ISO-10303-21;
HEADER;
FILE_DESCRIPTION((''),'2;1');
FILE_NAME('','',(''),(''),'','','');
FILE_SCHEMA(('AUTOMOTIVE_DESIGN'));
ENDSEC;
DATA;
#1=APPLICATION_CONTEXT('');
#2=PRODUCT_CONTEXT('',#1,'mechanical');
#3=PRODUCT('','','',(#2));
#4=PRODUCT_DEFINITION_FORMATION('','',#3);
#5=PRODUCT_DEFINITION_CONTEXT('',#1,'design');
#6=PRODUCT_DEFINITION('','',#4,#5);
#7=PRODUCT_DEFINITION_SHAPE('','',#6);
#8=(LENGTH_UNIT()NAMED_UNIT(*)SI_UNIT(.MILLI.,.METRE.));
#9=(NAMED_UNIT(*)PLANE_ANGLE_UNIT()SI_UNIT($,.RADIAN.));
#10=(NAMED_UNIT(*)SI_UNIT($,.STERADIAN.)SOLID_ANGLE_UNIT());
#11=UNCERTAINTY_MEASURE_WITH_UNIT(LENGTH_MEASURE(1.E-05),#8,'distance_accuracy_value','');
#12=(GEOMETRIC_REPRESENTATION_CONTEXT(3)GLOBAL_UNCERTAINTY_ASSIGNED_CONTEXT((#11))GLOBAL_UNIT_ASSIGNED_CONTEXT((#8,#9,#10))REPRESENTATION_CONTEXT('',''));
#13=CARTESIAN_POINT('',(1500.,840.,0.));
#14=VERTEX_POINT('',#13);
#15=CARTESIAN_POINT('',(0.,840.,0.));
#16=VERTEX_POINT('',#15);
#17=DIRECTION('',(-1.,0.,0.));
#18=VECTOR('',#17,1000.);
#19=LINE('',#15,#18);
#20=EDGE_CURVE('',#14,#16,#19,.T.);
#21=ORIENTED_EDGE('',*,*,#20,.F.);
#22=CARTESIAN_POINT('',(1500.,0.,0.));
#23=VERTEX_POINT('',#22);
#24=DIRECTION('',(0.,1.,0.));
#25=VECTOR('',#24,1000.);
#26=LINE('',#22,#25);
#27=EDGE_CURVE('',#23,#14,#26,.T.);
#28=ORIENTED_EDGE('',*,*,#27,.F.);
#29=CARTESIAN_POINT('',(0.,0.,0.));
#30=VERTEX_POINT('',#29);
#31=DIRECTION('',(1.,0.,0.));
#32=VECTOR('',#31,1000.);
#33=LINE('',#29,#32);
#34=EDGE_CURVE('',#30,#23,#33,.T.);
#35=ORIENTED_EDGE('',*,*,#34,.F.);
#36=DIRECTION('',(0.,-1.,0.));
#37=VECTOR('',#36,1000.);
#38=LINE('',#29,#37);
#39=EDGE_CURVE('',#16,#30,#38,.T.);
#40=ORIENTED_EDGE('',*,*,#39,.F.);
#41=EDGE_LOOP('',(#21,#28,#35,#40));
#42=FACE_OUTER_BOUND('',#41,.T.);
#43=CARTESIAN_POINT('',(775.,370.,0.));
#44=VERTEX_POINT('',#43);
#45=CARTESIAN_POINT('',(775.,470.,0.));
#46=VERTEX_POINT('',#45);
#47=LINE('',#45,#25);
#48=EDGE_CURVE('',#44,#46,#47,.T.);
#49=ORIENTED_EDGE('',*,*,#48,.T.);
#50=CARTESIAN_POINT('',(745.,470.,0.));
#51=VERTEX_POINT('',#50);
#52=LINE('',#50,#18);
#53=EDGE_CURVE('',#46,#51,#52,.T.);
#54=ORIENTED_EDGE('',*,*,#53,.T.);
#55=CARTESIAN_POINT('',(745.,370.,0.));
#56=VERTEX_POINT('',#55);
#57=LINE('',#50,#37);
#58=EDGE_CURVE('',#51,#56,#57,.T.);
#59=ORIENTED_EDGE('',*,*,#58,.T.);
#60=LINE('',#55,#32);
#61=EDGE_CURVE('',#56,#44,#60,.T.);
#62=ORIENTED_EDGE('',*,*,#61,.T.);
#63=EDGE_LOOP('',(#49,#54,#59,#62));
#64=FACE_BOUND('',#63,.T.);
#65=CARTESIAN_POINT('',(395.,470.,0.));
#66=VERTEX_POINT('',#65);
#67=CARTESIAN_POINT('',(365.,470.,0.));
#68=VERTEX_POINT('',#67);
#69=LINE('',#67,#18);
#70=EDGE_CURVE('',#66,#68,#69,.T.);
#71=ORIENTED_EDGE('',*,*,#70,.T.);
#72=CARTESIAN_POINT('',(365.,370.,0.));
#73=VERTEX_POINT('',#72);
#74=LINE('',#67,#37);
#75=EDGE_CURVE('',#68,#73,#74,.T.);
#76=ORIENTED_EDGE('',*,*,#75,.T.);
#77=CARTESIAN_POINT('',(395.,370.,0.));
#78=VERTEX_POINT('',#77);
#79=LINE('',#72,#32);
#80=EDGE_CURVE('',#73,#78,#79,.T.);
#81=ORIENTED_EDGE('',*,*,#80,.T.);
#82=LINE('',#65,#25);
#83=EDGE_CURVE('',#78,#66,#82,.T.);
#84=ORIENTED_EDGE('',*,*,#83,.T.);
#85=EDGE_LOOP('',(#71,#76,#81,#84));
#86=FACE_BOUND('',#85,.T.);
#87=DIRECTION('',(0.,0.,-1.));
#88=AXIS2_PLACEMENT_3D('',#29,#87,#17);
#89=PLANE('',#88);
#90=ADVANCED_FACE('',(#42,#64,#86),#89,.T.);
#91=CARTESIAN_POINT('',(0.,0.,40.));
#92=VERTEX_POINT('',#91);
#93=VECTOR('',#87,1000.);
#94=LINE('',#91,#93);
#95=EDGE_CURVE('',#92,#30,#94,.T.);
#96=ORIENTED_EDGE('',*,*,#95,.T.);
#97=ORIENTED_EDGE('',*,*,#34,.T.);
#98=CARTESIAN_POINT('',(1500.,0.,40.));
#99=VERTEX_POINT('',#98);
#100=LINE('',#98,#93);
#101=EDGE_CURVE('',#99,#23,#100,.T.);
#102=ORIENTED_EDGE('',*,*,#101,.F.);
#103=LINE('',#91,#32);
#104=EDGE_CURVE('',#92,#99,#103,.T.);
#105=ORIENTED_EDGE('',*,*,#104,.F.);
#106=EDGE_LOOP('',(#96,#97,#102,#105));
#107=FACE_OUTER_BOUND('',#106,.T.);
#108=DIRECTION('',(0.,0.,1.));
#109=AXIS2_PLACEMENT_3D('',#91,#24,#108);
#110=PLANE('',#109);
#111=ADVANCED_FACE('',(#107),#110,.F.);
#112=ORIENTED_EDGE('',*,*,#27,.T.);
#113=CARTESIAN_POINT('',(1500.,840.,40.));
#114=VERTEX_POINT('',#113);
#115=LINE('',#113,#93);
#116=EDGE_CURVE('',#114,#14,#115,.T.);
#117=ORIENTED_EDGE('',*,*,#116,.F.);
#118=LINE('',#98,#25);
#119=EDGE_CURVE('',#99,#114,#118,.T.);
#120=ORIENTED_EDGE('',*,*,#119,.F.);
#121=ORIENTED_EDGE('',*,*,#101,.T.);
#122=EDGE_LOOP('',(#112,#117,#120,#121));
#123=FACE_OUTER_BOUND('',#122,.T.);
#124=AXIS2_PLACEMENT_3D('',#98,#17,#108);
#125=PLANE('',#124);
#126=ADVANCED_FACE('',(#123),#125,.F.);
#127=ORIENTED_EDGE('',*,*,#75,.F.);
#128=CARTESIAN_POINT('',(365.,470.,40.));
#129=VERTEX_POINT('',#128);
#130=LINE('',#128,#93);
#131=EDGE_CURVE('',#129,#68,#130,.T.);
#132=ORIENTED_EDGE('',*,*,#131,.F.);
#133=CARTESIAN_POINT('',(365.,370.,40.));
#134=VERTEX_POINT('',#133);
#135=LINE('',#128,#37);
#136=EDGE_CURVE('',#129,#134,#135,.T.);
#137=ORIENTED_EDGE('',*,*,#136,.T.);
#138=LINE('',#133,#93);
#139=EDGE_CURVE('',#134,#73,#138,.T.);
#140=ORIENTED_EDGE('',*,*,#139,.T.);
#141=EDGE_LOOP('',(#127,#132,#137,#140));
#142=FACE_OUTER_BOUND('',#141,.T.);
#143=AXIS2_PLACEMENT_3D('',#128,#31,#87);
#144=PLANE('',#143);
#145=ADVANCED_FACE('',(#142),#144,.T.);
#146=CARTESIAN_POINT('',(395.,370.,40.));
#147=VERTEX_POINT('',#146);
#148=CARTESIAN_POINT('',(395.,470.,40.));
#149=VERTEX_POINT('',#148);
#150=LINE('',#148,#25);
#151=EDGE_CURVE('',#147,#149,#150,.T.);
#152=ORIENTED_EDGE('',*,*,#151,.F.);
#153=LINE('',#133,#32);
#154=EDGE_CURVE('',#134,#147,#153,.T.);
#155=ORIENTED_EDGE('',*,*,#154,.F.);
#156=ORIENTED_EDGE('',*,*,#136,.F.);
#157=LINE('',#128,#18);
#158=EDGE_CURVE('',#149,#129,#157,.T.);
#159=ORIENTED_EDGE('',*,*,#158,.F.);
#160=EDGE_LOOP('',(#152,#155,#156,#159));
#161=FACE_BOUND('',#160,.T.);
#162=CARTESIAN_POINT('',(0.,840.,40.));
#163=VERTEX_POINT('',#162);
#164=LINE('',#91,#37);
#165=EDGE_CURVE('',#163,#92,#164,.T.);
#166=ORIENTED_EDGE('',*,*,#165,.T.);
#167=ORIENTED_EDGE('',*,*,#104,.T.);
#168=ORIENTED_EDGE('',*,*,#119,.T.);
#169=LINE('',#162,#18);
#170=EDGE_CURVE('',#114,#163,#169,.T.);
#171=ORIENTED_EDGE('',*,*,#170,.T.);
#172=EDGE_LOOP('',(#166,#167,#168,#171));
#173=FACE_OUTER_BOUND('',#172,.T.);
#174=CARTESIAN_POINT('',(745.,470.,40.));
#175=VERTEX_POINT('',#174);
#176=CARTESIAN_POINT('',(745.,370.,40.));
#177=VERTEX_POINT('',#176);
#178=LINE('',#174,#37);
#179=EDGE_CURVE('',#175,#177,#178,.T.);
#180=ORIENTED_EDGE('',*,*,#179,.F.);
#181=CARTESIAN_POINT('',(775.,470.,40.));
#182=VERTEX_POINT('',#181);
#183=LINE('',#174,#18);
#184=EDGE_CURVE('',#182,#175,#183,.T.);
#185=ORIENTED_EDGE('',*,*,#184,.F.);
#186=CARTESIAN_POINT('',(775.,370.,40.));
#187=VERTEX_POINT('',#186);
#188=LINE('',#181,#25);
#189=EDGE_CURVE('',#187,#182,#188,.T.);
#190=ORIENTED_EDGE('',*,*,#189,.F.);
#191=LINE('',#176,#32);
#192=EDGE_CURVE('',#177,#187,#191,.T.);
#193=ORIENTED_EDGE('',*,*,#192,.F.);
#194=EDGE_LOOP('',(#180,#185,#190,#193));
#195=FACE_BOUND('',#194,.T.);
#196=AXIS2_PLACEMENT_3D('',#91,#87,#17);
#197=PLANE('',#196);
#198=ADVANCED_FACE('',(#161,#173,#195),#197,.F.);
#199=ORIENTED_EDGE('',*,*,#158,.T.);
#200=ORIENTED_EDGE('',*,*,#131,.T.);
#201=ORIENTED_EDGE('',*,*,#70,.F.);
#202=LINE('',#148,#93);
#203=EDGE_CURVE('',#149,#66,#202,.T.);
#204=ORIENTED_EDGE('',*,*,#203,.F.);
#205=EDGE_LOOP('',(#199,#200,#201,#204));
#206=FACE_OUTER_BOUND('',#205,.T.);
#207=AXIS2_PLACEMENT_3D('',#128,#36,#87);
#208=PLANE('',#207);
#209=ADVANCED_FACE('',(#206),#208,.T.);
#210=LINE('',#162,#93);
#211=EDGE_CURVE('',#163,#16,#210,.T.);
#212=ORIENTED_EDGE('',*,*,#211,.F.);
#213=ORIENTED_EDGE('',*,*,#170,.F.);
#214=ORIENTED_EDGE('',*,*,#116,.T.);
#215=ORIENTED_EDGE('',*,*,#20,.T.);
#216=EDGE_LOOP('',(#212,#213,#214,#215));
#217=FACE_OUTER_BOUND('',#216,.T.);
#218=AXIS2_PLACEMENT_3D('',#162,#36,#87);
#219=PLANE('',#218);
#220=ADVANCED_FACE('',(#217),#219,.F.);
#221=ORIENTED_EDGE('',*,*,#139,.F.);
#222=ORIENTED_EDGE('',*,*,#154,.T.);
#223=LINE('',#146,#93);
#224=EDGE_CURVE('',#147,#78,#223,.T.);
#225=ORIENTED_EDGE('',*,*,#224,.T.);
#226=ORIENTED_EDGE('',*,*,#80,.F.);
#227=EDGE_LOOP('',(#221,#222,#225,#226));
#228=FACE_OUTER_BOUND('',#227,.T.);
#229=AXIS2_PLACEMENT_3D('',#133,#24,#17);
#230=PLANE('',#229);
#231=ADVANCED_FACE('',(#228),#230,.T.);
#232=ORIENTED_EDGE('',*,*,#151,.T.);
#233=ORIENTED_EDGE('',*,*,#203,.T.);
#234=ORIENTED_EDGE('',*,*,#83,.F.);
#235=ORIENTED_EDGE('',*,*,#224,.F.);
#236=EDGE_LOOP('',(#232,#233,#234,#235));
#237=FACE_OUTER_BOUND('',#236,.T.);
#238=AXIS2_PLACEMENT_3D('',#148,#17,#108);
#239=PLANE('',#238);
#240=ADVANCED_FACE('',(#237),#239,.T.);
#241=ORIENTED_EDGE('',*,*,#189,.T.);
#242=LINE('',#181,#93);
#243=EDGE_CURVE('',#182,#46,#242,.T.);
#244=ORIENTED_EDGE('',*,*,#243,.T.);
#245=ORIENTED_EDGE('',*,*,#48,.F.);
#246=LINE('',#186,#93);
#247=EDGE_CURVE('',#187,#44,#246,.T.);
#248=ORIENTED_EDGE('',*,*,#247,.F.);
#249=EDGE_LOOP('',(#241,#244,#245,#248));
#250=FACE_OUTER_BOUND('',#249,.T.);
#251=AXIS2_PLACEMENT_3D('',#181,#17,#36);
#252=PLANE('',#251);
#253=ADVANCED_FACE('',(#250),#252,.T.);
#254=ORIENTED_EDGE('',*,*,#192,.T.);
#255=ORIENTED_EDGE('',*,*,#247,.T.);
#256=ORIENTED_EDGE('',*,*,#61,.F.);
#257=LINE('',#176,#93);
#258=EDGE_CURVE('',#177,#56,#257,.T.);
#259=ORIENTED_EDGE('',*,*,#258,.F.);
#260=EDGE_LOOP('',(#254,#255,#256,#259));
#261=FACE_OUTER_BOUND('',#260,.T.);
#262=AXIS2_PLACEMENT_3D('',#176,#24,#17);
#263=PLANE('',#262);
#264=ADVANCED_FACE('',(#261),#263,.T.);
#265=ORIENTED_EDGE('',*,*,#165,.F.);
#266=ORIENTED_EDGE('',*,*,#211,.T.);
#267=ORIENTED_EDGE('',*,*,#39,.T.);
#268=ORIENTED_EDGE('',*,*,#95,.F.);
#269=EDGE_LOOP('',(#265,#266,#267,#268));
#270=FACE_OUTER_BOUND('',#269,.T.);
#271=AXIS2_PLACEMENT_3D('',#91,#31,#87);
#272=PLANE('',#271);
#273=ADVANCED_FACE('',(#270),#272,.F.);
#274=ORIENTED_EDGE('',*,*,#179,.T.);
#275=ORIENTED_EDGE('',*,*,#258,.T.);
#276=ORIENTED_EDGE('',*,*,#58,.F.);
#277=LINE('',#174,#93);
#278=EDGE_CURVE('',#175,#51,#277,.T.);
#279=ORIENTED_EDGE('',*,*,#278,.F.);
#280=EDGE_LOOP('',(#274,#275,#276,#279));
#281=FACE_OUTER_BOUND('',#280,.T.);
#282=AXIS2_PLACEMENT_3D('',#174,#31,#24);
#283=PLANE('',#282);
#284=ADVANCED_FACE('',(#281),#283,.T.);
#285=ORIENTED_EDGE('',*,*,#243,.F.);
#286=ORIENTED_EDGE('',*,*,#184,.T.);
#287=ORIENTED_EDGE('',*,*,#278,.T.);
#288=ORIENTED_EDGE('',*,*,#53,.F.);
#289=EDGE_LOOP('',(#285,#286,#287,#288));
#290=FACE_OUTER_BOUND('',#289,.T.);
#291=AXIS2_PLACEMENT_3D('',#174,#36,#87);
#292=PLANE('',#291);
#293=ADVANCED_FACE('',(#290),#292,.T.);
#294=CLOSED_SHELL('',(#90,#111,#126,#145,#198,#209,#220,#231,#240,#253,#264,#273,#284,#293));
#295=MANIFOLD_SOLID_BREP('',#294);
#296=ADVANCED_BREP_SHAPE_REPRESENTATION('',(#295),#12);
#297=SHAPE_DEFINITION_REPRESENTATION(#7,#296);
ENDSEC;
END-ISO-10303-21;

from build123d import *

# Parameters (mm, degrees)
SKETCH1_W           = 1500
SKETCH1_H           = 840
SKETCH1_W_2         = 30
SKETCH1_H_2         = 100
BOSS_EXTRUDE1_DEPTH = 40


with BuildPart() as part:
    # Sketch1 → Boss-Extrude1 (new body)
    with BuildSketch(Plane.XY):
        with Locations((750, 420)):
            Rectangle(SKETCH1_W, SKETCH1_H)
        with Locations((380, 420)):
            Rectangle(SKETCH1_W_2, SKETCH1_H_2, mode=Mode.SUBTRACT)
        with Locations((760, 420)):
            Rectangle(SKETCH1_W_2, SKETCH1_H_2, mode=Mode.SUBTRACT)
    extrude(amount=BOSS_EXTRUDE1_DEPTH)


solid = part.part
